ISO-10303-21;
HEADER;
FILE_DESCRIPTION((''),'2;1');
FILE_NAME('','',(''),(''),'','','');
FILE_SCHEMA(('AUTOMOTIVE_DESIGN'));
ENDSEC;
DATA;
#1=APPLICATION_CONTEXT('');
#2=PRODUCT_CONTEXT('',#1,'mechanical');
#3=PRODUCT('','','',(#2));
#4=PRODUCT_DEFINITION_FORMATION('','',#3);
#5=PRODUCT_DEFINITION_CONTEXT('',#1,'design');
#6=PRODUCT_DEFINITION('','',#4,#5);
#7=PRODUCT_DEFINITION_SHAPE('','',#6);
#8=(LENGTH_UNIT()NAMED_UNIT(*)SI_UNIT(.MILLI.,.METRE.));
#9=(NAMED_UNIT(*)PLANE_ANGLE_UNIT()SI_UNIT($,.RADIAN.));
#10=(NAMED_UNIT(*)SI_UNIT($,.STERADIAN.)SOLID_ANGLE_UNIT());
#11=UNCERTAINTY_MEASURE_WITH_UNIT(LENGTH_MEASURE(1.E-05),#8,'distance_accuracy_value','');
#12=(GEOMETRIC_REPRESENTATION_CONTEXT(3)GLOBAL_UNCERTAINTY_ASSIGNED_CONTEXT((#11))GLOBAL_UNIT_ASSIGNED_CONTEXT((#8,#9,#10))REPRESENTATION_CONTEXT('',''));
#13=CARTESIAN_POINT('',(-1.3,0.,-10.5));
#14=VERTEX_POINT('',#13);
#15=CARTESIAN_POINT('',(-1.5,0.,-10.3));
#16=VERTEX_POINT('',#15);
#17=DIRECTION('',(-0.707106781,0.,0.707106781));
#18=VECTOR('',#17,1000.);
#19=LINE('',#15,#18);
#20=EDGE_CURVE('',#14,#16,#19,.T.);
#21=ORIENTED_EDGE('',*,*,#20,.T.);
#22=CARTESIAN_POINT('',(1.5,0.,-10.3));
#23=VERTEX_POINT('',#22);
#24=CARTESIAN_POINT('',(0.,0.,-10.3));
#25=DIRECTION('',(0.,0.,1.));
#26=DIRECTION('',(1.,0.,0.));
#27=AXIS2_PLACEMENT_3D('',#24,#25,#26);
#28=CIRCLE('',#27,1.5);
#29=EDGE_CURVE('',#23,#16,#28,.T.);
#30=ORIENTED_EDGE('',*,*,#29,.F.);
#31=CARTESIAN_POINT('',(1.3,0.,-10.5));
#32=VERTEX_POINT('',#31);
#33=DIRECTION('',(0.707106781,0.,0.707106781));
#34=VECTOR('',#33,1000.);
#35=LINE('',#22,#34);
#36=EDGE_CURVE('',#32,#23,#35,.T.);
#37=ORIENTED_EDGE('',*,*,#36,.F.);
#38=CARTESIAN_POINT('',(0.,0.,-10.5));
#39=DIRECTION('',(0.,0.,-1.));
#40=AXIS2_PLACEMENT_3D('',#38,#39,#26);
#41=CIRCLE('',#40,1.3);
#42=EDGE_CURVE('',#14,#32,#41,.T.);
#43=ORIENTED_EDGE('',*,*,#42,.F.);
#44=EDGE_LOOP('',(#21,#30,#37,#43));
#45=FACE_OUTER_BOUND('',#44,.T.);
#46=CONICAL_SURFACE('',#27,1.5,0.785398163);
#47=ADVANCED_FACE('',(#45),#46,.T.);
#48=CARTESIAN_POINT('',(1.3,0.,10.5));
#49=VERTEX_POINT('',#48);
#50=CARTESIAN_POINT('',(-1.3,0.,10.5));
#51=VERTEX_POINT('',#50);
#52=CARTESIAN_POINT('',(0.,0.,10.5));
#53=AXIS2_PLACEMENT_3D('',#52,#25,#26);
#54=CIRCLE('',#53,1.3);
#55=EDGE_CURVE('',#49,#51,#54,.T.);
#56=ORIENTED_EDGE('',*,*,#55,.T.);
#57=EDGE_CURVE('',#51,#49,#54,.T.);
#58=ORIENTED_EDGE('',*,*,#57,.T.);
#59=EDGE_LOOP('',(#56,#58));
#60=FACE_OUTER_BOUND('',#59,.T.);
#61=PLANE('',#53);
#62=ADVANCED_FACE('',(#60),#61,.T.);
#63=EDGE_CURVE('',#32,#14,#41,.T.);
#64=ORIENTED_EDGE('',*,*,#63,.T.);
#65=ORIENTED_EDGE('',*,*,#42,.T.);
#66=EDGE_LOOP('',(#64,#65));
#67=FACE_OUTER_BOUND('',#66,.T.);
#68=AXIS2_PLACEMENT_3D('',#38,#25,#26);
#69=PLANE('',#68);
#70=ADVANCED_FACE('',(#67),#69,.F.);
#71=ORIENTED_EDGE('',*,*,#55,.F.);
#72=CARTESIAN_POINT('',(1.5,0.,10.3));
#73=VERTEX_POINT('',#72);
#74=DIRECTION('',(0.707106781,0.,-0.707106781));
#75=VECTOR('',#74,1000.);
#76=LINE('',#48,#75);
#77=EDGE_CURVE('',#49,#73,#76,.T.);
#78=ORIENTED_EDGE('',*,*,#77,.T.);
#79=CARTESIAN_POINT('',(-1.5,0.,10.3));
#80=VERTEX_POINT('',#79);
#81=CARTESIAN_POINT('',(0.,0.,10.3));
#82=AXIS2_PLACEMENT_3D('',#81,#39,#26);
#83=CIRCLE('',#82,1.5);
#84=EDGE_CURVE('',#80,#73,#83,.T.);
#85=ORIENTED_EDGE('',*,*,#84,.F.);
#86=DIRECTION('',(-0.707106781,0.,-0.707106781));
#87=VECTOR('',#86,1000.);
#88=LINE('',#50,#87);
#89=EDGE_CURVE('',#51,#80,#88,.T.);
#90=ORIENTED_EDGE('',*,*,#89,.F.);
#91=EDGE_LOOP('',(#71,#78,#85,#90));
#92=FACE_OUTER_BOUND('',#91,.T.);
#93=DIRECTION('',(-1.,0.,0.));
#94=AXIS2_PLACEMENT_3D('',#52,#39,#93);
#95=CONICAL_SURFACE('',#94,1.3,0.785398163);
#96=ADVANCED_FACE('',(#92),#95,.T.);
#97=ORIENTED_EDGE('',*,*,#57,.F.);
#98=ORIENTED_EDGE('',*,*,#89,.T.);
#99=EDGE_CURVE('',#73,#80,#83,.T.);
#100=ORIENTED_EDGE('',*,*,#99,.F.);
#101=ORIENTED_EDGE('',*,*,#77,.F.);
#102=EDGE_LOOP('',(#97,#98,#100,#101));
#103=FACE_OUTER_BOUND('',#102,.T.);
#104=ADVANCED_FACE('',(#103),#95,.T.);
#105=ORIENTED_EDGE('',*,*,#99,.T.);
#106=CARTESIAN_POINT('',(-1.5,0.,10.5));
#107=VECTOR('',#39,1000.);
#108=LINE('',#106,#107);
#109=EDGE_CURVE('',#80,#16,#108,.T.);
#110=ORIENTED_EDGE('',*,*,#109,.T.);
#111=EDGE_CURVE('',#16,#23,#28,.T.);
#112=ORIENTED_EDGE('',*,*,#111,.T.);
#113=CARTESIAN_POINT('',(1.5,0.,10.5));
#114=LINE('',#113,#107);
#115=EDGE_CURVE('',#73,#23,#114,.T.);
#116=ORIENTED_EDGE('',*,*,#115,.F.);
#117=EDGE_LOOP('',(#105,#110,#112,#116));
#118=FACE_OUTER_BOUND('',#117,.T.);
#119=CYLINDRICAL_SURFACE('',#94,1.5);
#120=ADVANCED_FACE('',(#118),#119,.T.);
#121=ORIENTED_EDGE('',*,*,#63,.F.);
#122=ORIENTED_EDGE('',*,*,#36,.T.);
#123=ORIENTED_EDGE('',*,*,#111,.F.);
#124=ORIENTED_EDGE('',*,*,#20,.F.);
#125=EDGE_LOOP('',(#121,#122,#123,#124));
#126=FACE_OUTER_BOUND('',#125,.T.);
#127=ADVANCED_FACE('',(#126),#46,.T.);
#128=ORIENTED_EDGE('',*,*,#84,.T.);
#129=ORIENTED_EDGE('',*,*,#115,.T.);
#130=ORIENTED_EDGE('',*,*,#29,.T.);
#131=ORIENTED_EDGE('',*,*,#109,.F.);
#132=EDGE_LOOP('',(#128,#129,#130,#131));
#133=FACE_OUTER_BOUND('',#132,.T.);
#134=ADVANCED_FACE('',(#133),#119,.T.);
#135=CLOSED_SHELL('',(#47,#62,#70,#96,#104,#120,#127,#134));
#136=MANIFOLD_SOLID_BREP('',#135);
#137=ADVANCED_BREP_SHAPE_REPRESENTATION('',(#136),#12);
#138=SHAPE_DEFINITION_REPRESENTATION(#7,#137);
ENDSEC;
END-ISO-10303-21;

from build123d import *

# Parameters (mm, degrees)
PIN_PROFILE_3_R          = 1.5
PIN_BODY_3X21_DEPTH      = 10.5
END_CHAMFERS_0_2X45_SIZE = 0.2


with BuildPart() as part:
    # Pin Profile Ø3 → Pin Body Ø3x21 (new, symmetric)
    with BuildSketch(Plane.XY):
        with Locations(Location((0, 0, 0), (0, 0, 180))):
            Circle(PIN_PROFILE_3_R)
    extrude(amount=PIN_BODY_3X21_DEPTH, both=True)

    # End Chamfers 0.2x45°
    end_chamfers_0_2x45_edges = [part.edges().sort_by_distance(p)[0] for p in [
        (1.5, 0, -10.5),
        (1.5, 0, 10.5),
    ]]
    chamfer(end_chamfers_0_2x45_edges, length=END_CHAMFERS_0_2X45_SIZE)


solid = part.part
